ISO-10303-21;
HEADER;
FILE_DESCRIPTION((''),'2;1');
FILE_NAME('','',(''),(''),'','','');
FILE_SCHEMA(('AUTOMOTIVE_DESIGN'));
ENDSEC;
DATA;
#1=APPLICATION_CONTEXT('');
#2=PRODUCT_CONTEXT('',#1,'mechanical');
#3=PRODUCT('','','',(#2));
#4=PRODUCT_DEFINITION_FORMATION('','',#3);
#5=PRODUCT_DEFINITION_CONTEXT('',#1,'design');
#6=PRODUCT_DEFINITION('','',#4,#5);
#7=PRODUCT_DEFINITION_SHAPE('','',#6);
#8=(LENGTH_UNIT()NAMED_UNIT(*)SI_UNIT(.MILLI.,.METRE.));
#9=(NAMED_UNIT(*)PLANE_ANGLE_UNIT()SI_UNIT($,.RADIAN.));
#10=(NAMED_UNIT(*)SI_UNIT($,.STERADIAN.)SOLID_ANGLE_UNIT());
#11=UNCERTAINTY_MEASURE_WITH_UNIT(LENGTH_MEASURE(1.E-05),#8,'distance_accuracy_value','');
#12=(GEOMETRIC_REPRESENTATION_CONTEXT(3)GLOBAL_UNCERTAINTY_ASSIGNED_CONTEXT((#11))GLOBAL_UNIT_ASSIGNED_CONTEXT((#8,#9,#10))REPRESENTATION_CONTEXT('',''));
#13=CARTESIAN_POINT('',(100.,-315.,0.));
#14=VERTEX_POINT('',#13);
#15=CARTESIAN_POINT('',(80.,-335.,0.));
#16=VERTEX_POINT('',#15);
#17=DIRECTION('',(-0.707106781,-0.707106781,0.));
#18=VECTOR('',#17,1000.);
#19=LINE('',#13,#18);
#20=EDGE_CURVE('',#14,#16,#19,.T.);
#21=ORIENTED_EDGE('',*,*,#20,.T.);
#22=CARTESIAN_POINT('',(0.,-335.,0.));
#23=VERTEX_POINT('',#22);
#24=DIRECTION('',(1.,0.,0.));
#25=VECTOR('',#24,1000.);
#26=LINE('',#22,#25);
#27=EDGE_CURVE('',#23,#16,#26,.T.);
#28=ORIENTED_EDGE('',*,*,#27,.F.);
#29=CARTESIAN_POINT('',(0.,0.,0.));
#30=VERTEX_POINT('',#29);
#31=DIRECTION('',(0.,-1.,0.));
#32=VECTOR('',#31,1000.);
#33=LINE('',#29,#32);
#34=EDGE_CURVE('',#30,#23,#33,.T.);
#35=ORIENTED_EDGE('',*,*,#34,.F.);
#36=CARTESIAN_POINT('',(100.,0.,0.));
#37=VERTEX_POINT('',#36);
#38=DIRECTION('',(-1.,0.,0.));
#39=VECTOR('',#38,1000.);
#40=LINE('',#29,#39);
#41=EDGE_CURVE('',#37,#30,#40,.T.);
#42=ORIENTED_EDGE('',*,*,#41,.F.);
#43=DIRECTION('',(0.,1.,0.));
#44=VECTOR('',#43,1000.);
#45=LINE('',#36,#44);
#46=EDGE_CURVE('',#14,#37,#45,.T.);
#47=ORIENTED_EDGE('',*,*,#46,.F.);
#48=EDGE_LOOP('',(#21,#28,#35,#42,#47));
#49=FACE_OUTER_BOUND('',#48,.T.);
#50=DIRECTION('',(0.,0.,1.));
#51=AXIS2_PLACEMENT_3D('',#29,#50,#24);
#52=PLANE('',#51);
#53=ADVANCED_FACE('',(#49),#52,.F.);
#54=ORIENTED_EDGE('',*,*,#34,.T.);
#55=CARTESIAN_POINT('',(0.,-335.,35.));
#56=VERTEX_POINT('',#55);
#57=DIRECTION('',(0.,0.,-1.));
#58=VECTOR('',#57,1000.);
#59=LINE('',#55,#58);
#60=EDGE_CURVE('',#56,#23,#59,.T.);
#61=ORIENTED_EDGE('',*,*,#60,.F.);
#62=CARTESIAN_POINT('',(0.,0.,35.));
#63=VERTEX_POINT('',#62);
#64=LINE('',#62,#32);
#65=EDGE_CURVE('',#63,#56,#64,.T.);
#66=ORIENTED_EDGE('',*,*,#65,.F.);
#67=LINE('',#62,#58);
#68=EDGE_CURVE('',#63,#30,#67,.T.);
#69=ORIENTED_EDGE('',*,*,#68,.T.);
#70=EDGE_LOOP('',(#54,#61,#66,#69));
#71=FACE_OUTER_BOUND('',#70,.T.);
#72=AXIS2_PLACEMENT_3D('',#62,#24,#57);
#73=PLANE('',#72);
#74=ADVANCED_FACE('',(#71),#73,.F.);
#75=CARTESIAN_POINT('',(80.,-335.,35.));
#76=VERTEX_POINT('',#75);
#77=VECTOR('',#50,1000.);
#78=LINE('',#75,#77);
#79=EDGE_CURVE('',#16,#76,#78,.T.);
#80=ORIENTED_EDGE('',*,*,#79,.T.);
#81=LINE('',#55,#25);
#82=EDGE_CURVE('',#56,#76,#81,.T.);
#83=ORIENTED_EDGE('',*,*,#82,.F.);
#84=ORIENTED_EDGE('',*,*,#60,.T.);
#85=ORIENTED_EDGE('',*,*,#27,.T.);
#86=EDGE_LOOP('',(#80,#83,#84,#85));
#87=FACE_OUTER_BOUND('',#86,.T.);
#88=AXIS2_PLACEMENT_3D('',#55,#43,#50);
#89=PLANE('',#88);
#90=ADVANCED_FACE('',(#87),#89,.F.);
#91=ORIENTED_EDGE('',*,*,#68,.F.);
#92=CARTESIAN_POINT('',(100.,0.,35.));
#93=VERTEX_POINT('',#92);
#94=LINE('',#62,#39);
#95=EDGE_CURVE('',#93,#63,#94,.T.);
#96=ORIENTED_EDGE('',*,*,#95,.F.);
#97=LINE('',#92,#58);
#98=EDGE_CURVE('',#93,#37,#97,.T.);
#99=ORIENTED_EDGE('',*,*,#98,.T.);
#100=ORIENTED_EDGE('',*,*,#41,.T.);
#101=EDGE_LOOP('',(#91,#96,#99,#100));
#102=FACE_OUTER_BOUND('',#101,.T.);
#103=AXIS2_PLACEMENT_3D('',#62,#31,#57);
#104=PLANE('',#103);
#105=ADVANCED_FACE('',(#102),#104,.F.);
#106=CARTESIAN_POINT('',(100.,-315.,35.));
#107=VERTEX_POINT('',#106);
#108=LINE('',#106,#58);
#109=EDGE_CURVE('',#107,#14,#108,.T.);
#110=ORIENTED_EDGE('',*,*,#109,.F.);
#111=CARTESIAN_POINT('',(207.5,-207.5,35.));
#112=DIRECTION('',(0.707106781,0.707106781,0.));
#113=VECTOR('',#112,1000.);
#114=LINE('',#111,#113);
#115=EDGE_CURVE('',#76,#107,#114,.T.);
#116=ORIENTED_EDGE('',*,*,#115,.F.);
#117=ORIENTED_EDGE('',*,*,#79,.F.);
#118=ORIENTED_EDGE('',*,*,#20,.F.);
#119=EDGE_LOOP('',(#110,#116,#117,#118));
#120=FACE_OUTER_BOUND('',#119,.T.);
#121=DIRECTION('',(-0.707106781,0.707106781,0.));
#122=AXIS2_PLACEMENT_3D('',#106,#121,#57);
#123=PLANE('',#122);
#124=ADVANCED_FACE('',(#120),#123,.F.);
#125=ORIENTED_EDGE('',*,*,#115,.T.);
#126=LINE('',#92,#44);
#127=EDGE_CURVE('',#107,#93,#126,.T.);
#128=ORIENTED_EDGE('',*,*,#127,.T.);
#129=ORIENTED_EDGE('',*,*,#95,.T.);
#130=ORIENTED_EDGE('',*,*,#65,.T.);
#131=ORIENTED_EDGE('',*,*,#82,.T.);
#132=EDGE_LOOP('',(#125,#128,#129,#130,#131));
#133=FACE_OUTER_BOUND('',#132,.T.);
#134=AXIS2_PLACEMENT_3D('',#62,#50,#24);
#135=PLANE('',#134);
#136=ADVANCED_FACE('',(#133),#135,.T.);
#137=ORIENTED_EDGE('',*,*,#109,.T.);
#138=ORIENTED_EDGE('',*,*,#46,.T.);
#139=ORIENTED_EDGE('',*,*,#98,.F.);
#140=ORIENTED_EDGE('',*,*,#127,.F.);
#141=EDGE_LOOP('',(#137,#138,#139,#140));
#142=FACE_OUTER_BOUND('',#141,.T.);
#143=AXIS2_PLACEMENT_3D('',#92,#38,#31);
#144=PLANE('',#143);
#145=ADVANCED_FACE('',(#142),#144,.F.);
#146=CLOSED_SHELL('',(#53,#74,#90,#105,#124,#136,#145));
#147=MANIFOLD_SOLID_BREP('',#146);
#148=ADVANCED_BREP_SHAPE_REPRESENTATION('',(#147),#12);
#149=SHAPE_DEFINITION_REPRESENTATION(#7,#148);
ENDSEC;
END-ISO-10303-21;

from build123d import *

# Parameters (mm, degrees)
SKETCH1_W           = 100
SKETCH1_H           = 335
BOSS_EXTRUDE1_DEPTH = 35
CHAMFER1_SIZE       = 20


with BuildPart() as part:
    # Sketch1 → Boss-Extrude1 (new body)
    with BuildSketch(Plane.XY):
        with Locations((50, -167.5)):
            Rectangle(SKETCH1_W, SKETCH1_H)
    extrude(amount=BOSS_EXTRUDE1_DEPTH)

    # Chamfer1
    chamfer1_edges = [part.edges().sort_by_distance(p)[0] for p in [
        (100, -335, 17.5),
    ]]
    chamfer(chamfer1_edges, length=CHAMFER1_SIZE)


solid = part.part
